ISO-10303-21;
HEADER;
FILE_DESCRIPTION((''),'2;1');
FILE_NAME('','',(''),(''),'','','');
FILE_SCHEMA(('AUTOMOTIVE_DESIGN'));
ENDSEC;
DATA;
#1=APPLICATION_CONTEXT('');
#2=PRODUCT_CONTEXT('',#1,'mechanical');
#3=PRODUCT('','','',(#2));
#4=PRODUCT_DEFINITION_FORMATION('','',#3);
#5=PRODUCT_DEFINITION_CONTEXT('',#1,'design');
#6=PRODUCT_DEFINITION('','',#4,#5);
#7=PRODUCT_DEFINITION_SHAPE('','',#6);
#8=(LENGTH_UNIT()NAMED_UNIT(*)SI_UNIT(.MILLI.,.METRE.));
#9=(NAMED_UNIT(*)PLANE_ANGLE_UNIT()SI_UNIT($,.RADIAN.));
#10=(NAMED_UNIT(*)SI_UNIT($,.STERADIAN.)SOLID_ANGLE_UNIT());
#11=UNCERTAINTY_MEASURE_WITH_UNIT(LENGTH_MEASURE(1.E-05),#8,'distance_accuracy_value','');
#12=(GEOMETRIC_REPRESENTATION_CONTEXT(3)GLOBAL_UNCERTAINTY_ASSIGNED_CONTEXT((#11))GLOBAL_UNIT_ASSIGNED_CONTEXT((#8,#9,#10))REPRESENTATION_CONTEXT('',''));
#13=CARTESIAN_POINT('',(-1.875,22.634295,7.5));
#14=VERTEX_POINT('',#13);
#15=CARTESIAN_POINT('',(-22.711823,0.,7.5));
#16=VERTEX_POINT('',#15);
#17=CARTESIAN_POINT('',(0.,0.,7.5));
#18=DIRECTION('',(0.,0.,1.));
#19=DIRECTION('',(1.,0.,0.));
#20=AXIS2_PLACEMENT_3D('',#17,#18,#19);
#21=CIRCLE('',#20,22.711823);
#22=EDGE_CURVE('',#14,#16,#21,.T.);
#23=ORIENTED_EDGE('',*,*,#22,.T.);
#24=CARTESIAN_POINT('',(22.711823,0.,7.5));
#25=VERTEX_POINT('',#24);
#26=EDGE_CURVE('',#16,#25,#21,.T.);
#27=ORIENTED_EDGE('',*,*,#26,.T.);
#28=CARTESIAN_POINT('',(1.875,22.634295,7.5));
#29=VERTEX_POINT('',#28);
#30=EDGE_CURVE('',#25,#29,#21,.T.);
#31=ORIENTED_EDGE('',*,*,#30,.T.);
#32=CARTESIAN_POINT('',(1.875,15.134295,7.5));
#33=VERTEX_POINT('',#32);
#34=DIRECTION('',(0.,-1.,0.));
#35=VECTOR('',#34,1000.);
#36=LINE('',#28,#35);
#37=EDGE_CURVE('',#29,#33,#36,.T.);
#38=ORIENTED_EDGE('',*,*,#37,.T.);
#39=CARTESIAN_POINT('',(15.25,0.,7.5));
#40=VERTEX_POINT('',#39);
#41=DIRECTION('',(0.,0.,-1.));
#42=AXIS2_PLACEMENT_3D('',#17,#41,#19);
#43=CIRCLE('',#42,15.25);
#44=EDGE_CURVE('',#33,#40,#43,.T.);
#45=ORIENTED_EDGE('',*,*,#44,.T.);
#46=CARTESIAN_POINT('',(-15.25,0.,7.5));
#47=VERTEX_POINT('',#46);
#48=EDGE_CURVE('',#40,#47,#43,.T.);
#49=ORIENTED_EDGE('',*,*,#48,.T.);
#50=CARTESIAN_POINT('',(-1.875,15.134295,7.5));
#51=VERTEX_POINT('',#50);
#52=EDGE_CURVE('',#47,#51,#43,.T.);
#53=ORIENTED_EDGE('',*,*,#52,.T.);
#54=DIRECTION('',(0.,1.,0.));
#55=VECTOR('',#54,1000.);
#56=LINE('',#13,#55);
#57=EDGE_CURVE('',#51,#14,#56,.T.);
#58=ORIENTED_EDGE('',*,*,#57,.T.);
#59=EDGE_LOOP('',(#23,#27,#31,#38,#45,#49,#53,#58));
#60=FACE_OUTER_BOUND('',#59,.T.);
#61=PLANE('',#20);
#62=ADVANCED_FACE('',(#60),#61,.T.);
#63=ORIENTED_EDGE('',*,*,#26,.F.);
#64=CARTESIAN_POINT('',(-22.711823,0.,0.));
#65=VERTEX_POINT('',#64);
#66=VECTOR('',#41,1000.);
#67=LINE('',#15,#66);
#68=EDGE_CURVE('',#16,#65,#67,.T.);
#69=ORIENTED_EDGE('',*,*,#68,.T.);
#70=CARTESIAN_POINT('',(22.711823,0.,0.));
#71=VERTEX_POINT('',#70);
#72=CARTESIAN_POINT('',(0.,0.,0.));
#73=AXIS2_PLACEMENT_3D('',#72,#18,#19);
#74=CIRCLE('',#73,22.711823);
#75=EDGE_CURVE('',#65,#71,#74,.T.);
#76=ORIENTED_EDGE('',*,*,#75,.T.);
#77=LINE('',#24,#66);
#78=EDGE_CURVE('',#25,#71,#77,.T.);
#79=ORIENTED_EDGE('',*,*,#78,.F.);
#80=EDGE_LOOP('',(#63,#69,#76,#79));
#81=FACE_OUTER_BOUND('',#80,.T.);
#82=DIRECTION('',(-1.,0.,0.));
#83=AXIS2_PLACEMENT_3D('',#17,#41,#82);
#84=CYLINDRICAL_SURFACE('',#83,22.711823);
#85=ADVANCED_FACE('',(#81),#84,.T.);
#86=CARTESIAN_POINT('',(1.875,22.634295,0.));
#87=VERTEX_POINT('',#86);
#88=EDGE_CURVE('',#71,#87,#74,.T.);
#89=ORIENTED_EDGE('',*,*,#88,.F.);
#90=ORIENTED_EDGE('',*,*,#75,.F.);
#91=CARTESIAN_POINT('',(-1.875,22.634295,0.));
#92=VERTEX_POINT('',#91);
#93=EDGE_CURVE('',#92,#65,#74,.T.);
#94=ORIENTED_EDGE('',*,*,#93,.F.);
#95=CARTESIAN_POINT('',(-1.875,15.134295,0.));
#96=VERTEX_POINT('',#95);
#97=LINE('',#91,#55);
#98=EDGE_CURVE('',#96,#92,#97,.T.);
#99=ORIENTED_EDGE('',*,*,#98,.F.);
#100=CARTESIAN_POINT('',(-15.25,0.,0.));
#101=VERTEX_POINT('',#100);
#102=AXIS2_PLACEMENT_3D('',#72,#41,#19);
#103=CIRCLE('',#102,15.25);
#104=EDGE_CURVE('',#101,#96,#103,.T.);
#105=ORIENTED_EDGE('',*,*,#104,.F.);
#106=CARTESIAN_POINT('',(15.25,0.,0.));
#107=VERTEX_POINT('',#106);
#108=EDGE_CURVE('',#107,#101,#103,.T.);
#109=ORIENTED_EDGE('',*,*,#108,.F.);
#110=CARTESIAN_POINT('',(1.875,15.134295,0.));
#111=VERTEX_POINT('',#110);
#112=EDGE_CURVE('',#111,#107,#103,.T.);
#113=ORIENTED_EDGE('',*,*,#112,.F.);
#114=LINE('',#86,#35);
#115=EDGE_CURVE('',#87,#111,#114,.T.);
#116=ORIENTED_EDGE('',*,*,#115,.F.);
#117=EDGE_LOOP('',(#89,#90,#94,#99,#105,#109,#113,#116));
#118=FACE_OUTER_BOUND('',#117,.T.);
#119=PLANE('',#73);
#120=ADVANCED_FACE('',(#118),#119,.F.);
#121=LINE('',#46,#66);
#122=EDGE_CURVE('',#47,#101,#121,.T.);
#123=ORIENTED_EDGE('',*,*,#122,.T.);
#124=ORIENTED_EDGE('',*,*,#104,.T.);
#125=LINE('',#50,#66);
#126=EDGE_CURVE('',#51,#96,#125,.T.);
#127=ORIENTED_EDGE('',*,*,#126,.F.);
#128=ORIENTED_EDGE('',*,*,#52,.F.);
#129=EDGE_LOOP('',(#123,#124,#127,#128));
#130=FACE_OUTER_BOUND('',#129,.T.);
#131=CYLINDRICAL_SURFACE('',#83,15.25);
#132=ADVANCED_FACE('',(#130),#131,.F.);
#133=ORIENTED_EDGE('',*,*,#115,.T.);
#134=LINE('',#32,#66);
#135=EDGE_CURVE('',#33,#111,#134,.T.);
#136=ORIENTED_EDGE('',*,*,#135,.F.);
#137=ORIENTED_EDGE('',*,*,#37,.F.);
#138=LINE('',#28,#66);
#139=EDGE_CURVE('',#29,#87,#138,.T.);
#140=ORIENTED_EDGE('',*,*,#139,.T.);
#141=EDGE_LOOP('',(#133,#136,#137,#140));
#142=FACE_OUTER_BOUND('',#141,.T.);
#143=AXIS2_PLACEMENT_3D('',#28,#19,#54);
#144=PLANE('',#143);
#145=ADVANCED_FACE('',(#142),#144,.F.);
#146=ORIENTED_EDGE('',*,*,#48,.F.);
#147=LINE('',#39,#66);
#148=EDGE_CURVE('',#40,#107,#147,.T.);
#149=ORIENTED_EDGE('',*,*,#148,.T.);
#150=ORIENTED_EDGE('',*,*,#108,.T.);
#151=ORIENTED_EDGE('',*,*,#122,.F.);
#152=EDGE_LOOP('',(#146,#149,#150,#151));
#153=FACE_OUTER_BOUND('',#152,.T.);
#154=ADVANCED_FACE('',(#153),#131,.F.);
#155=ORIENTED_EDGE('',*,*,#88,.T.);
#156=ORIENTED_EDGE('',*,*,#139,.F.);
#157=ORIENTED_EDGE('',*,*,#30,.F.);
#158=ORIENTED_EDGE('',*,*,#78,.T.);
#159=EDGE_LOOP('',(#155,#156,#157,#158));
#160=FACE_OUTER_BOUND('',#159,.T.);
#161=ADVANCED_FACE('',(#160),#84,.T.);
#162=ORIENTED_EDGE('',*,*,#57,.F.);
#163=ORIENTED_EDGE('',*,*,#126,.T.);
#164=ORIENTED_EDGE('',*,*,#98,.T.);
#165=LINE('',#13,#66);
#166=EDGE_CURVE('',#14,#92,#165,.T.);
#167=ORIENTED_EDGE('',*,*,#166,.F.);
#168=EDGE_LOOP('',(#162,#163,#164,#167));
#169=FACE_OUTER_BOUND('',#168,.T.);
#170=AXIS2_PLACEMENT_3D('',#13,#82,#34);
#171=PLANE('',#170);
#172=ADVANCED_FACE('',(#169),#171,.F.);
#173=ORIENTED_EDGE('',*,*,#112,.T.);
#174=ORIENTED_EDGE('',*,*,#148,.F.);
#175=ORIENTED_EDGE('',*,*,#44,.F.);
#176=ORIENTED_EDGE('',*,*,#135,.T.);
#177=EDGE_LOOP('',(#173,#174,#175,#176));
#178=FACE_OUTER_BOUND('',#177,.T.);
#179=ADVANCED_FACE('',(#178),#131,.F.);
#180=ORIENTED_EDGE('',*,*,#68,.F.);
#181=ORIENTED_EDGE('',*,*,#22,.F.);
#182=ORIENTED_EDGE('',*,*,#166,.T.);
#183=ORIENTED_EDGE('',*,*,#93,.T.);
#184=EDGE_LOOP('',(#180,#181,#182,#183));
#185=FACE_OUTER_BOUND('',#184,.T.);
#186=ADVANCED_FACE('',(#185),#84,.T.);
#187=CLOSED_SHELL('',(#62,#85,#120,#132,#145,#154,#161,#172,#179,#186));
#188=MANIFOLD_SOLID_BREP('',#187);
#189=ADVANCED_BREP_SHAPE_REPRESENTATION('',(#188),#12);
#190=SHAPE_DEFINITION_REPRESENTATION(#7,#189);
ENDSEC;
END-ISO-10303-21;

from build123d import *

# Parameters (mm, degrees)
EXTRUDE_1_DEPTH = 7.5


with BuildPart() as part:
    # 草图1 → 拉伸1 (new body)
    with BuildSketch(Plane.XY):
        with BuildLine():
            Line((-1.875, 22.634294665), (-1.875, 15.134294665))
            ThreePointArc((-1.875, 15.134294665), (0, -15.25), (1.875, 15.134294665))
            Line((1.875, 15.134294665), (1.875, 22.634294665))
            ThreePointArc((1.875, 22.634294665), (0, -22.711823352), (-1.875, 22.634294665))
        make_face()
    extrude(amount=EXTRUDE_1_DEPTH)


solid = part.part
